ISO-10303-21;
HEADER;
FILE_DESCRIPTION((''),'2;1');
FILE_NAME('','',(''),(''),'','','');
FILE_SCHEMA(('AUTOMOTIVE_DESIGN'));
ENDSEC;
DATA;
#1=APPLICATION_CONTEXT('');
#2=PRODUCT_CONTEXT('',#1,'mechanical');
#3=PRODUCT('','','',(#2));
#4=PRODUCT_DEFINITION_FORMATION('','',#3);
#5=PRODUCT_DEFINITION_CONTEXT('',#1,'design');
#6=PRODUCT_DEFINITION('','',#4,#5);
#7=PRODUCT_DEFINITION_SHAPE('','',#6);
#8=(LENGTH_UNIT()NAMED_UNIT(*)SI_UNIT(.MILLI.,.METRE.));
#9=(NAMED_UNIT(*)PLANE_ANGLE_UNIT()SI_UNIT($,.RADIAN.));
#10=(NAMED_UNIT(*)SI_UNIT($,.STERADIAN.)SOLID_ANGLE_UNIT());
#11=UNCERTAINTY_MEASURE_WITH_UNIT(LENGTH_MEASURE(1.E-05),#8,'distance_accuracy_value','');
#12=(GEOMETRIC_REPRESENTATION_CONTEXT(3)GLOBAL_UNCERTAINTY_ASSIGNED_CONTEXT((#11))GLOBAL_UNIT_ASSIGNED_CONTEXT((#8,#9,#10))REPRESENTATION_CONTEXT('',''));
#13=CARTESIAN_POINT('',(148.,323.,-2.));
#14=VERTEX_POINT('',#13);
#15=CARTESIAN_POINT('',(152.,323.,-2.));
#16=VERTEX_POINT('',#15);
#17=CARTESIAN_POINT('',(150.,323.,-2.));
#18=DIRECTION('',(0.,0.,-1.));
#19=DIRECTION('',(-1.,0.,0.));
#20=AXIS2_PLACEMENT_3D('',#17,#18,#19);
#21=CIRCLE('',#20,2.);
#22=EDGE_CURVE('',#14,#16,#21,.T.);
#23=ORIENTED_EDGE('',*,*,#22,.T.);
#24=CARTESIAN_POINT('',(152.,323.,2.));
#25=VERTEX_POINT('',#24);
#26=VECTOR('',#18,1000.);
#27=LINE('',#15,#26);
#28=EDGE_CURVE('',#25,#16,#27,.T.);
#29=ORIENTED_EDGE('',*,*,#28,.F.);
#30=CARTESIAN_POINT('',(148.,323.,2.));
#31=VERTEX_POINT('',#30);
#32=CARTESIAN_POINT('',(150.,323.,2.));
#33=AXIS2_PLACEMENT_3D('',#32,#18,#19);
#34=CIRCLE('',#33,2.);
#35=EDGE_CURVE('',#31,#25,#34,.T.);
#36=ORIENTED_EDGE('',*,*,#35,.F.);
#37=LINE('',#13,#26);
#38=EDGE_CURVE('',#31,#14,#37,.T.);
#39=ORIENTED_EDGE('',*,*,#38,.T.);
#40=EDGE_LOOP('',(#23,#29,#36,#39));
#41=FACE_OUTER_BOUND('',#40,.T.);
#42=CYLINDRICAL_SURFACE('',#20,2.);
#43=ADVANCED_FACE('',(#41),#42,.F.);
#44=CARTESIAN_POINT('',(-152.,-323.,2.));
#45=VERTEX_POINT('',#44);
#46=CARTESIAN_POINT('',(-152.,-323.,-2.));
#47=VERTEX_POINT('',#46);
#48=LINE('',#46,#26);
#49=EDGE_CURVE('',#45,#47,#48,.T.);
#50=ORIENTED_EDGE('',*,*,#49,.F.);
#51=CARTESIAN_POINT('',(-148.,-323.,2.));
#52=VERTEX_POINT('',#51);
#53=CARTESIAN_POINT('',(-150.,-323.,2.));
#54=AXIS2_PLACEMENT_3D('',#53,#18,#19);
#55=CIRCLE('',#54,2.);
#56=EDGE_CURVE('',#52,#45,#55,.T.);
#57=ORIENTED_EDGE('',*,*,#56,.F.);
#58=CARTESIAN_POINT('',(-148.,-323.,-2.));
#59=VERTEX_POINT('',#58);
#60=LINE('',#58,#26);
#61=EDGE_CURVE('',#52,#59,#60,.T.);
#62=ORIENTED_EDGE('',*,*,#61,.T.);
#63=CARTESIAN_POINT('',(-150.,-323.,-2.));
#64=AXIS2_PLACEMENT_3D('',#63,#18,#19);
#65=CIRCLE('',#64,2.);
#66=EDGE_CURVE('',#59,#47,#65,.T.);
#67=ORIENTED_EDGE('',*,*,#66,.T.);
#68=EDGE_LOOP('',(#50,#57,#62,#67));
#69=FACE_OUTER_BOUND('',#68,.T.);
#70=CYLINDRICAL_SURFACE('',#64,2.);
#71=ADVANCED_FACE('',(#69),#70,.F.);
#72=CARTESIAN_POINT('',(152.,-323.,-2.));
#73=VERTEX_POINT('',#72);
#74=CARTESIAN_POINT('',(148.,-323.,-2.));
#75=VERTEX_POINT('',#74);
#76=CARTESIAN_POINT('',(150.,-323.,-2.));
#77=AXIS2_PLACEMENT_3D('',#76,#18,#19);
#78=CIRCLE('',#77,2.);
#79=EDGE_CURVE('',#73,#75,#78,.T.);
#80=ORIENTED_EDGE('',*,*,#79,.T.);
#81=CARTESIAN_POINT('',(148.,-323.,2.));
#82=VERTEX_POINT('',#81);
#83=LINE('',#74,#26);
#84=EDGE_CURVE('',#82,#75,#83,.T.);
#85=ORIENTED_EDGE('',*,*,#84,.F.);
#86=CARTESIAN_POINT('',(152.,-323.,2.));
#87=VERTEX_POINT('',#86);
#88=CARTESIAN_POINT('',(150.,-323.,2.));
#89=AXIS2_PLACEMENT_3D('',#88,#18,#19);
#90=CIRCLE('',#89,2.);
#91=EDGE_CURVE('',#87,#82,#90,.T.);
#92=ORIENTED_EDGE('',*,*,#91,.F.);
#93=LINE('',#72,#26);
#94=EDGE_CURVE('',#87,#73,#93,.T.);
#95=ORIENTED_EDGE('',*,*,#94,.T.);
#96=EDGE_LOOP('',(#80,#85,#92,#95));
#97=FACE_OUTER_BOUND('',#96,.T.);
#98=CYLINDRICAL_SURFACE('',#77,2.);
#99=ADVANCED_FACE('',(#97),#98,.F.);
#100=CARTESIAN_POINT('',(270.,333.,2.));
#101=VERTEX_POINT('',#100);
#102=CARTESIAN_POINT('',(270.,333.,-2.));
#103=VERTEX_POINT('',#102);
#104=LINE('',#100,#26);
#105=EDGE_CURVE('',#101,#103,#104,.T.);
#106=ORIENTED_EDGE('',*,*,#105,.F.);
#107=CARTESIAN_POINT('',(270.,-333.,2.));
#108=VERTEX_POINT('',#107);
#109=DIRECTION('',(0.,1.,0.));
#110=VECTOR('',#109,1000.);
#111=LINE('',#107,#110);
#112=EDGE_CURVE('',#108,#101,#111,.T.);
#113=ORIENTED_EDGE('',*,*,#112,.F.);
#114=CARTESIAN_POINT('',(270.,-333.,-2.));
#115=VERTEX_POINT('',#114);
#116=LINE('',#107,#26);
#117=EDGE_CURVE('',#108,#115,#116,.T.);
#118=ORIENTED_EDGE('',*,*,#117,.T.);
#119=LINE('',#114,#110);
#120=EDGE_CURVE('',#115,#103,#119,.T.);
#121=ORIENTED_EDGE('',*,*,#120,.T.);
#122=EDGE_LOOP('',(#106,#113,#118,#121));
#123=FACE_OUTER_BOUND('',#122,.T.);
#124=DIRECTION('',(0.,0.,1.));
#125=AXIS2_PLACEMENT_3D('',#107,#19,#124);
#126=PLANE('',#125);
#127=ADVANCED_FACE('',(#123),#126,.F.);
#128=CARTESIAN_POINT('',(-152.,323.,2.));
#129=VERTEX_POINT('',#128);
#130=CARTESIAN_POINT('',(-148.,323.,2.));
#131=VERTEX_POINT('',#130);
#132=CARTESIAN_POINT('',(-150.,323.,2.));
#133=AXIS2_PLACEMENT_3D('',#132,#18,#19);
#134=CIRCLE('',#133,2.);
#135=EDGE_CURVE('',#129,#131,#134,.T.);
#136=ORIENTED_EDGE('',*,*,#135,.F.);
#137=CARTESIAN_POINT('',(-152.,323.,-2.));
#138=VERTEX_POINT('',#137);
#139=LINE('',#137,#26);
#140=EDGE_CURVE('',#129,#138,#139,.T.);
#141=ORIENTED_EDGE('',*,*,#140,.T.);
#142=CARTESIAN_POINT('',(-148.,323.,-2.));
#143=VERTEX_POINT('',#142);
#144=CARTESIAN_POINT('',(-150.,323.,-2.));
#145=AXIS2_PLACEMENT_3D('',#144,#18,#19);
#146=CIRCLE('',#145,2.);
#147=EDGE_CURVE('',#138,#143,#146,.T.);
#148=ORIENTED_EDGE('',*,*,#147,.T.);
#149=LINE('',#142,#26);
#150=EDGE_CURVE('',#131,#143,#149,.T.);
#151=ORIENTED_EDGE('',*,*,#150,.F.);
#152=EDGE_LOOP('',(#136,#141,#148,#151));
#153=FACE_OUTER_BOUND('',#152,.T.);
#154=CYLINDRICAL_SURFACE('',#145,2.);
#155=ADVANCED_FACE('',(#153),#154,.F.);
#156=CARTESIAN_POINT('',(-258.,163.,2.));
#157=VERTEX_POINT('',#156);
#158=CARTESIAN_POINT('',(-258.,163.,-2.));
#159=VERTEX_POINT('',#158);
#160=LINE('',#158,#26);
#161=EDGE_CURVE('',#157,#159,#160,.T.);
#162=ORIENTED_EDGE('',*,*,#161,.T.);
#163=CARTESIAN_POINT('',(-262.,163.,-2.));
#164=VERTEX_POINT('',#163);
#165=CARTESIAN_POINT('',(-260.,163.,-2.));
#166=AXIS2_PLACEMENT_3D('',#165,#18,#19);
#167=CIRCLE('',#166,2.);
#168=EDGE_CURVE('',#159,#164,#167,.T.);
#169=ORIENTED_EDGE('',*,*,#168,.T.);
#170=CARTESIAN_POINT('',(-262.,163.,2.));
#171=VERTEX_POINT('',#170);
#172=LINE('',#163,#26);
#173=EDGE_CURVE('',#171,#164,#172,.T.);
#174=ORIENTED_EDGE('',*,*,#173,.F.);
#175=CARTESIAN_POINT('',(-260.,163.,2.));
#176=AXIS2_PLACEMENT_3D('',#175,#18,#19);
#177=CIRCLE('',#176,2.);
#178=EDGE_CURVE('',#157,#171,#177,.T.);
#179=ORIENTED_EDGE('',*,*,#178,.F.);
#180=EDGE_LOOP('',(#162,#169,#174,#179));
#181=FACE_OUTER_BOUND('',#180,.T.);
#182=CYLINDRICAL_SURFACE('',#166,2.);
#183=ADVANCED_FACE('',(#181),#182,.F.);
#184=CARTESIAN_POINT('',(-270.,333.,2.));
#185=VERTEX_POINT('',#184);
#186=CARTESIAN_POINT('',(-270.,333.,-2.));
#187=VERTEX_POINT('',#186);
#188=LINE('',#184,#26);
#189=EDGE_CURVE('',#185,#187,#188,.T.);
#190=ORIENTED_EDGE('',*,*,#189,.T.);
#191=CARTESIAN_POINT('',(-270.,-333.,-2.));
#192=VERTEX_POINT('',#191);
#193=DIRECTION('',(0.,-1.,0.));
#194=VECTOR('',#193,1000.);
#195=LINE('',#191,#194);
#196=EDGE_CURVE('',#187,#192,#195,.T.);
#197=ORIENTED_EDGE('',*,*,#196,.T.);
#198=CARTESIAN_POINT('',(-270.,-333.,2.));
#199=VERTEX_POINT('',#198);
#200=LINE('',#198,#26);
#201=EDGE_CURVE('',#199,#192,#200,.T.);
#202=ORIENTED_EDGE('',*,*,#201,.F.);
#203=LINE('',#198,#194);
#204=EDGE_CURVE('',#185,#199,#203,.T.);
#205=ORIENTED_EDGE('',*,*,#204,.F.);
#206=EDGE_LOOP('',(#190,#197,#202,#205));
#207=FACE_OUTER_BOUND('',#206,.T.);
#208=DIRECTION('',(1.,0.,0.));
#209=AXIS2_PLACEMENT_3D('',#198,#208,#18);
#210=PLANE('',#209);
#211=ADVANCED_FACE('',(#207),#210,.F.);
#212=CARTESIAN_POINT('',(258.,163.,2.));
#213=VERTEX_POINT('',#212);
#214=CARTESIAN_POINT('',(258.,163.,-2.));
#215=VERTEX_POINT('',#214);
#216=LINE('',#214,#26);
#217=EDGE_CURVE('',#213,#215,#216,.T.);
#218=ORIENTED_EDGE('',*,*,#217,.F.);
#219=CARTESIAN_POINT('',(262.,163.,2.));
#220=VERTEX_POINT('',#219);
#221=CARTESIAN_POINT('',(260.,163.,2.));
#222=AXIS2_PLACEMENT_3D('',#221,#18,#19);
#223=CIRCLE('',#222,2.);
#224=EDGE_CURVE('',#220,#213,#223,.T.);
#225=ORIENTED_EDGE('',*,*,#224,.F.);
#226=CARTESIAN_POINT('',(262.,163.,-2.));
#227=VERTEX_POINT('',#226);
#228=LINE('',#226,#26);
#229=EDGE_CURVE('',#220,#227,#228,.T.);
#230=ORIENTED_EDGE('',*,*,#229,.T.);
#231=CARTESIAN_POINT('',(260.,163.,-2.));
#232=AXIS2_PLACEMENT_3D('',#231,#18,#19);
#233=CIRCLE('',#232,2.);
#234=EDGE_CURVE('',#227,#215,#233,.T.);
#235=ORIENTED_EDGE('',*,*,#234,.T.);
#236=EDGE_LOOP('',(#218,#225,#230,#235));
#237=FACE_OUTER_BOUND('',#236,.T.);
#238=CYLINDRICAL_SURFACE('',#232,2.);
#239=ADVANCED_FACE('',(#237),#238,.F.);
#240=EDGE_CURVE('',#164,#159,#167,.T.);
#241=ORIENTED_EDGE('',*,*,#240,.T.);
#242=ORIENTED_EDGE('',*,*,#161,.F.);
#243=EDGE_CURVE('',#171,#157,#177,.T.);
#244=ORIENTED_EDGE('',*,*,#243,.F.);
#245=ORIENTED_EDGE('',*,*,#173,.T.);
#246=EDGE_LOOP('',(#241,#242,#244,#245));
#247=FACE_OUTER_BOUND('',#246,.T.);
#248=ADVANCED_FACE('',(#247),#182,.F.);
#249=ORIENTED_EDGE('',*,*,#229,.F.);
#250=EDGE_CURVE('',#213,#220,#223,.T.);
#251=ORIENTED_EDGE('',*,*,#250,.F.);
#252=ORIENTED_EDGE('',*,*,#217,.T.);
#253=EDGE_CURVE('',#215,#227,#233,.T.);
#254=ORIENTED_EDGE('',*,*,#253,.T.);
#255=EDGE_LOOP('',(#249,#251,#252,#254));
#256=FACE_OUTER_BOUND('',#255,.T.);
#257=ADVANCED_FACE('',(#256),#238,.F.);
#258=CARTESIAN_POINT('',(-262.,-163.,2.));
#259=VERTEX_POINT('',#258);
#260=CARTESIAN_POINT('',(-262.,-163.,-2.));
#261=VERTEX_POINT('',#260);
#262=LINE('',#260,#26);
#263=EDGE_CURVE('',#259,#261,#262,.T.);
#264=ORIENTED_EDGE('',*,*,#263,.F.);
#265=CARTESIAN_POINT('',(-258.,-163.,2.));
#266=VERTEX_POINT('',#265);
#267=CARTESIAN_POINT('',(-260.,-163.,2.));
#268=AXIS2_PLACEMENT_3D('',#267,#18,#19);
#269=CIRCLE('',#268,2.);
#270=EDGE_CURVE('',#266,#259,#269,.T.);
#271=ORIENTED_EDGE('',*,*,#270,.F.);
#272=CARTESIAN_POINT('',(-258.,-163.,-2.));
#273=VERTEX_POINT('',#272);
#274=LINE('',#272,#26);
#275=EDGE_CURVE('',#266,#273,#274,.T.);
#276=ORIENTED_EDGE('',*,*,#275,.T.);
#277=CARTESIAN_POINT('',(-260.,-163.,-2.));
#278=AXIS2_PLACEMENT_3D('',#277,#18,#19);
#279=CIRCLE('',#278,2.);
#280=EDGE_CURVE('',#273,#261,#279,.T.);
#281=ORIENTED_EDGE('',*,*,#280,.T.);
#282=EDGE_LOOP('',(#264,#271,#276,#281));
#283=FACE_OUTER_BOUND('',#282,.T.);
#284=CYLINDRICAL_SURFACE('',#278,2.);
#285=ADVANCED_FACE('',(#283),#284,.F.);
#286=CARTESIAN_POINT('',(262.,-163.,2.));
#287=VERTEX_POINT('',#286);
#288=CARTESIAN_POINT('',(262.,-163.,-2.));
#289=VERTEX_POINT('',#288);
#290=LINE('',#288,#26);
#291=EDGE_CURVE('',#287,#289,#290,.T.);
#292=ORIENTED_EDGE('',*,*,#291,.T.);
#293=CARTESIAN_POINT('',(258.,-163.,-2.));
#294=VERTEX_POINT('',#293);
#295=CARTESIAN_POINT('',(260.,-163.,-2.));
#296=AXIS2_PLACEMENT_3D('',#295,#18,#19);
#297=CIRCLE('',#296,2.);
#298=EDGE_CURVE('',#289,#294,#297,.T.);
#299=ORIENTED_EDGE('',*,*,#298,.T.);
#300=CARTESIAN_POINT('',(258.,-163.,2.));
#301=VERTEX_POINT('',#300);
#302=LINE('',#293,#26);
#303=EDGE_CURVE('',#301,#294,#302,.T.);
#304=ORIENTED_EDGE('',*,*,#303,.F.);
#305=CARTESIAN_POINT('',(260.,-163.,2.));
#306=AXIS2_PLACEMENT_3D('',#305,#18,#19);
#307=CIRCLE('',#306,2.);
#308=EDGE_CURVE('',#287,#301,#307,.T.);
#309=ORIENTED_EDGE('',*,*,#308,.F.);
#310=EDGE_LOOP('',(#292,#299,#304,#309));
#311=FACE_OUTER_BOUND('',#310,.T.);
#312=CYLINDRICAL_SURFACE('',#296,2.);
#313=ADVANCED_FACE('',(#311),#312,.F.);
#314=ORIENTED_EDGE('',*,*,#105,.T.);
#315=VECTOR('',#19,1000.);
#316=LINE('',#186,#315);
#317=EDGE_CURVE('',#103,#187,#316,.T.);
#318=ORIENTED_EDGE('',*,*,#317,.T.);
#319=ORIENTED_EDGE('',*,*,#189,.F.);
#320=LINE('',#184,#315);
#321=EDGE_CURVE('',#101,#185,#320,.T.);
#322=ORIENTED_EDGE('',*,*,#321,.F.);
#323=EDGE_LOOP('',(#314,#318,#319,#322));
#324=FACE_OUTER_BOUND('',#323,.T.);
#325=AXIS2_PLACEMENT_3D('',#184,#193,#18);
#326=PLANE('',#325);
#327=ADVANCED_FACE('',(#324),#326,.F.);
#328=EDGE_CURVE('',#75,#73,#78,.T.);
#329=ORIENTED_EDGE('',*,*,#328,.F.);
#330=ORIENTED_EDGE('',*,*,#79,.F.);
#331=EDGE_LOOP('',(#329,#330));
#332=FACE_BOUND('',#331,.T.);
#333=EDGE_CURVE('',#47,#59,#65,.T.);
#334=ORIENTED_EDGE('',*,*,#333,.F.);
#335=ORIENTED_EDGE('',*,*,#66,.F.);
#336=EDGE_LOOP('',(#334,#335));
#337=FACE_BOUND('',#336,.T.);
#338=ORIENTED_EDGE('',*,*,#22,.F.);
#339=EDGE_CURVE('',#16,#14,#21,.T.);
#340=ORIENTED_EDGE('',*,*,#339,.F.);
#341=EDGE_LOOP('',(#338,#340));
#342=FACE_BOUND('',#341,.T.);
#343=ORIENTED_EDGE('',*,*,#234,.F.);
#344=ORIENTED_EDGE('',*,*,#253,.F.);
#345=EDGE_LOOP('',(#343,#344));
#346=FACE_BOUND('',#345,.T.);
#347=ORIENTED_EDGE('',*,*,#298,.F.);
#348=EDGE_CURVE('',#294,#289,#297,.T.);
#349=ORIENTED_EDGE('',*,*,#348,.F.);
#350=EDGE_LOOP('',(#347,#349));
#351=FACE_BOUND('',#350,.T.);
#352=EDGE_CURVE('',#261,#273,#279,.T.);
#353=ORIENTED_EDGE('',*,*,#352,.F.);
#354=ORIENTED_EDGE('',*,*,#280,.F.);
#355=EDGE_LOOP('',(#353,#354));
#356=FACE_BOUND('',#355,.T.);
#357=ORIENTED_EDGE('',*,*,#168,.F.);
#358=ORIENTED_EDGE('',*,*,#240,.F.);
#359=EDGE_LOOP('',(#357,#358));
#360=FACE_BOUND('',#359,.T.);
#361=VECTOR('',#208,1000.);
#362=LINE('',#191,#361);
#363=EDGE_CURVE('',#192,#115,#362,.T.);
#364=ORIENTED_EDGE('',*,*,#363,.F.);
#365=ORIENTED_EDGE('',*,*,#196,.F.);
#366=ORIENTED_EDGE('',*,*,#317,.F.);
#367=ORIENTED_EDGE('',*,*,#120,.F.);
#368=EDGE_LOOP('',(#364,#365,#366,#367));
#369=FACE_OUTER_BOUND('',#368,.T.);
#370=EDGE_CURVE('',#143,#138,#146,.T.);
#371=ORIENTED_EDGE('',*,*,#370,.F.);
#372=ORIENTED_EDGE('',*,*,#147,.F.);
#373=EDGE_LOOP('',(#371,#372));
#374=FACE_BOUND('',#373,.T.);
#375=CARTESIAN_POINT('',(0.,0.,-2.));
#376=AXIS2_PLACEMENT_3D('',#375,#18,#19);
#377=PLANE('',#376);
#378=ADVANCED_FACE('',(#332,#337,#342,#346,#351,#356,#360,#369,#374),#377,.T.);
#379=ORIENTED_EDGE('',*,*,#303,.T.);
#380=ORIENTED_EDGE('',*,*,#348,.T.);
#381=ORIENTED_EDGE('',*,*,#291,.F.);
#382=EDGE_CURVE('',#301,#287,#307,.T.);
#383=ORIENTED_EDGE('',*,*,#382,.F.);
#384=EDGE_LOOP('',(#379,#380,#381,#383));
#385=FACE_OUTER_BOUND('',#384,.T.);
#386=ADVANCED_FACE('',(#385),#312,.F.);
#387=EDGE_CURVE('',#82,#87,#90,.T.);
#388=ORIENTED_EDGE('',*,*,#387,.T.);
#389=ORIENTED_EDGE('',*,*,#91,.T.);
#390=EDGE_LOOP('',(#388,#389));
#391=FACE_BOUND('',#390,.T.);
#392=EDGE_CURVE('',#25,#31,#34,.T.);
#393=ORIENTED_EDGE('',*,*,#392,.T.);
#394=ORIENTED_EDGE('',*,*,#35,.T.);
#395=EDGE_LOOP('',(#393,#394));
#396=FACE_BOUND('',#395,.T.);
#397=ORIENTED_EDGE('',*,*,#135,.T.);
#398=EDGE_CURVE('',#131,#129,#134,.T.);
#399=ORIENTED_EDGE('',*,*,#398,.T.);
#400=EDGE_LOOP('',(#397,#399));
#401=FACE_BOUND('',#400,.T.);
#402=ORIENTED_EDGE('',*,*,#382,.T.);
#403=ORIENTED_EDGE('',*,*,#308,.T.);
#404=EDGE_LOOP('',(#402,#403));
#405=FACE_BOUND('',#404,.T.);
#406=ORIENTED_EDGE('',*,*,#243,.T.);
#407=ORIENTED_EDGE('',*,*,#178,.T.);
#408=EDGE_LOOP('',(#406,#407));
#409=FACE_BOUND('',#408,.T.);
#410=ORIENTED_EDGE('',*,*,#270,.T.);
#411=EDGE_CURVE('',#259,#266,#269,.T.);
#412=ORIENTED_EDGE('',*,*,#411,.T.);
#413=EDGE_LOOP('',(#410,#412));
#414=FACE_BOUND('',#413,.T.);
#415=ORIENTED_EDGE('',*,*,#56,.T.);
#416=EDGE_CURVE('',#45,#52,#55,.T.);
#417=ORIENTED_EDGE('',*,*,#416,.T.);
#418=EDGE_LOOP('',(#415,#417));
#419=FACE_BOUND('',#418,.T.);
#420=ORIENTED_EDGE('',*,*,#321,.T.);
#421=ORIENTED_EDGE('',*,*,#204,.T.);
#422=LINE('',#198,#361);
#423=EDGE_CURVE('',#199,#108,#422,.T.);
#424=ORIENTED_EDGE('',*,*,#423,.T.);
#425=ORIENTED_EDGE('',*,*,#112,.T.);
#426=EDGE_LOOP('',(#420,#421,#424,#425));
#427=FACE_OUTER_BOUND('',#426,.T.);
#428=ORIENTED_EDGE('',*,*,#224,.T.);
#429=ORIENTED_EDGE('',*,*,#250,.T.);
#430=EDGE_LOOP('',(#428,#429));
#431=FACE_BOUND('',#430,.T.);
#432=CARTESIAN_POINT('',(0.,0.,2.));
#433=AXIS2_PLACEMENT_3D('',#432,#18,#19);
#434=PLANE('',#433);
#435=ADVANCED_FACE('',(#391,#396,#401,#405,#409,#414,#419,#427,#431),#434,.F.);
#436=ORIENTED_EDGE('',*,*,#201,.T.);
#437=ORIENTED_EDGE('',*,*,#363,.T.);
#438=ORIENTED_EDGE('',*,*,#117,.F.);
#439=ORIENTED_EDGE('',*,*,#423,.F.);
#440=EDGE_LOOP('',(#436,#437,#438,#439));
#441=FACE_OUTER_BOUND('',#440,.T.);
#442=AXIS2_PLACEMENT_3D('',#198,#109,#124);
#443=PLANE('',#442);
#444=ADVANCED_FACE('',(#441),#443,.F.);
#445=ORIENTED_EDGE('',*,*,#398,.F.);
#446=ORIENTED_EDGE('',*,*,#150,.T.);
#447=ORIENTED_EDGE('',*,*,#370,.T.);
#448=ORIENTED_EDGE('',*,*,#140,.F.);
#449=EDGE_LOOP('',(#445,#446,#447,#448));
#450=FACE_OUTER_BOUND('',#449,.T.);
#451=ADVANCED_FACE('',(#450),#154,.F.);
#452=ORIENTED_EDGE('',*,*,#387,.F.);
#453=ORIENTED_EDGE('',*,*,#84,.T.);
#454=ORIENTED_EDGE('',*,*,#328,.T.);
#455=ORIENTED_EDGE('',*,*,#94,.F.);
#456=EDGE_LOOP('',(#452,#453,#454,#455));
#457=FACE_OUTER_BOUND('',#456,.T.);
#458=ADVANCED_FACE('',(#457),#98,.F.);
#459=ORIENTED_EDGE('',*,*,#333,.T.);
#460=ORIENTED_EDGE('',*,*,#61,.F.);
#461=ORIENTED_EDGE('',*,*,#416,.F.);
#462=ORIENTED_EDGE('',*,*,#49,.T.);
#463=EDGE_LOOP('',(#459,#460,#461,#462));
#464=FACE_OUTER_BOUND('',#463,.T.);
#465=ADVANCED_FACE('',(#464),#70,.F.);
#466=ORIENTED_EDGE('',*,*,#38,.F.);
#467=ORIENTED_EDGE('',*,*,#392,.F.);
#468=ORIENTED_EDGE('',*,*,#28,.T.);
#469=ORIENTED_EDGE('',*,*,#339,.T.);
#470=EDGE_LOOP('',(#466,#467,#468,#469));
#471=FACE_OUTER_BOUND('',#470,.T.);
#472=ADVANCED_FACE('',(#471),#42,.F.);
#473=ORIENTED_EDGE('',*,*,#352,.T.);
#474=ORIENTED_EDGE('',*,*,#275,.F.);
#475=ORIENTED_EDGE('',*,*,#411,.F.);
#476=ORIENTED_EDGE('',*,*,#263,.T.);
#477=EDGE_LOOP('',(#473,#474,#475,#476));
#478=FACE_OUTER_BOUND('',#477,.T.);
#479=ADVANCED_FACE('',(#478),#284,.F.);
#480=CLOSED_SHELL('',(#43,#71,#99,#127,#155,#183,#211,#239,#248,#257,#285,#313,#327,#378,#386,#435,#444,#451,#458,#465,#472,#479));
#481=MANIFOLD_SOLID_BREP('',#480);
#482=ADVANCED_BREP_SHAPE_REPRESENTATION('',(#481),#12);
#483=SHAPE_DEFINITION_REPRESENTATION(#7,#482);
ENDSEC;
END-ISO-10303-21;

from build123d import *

# Parameters (mm, degrees)
SKETCH_1_W            = 540
SKETCH_1_H            = 666
EXTRUDE_1_DEPTH       = 2
HOLE_WIZARD_4_0_4_1_D = 4
HOLE_WIZARD_4_0_4_2_D = 4


with BuildPart() as part:
    # 草图1 → 凸台-拉伸1 (new, symmetric)
    with BuildSketch(Plane.XY):
        Rectangle(SKETCH_1_W, SKETCH_1_H)
    extrude(amount=EXTRUDE_1_DEPTH, both=True)

    # Ø4.0 (4) 直径孔1 (through all)
    with Locations(Plane(origin=(0, 0, -2), x_dir=(-1, 0, 0), z_dir=(0, 0, -1))):
        with Locations((-260, 163), (-260, -163)):
            hole_wizard_4_0_4_1 = Hole(HOLE_WIZARD_4_0_4_1_D / 2)

    # Ø4.0 (4) 直径孔2 (through all)
    with Locations(Plane(origin=(0, 0, -2), x_dir=(-1, 0, 0), z_dir=(0, 0, -1))):
        with Locations((-150, 323), (150, 323)):
            hole_wizard_4_0_4_2 = Hole(HOLE_WIZARD_4_0_4_2_D / 2)

    # 镜向1: Ø4.0 (4) 直径孔2 across plane
    add(hole_wizard_4_0_4_2.mirror(Plane.ZX), mode=Mode.SUBTRACT)

    # 镜向2: Ø4.0 (4) 直径孔1 across plane
    add(hole_wizard_4_0_4_1.mirror(Plane(origin=(0, 0, 0), x_dir=(0, 0, 1), z_dir=(1, 0, 0))), mode=Mode.SUBTRACT)


solid = part.part
